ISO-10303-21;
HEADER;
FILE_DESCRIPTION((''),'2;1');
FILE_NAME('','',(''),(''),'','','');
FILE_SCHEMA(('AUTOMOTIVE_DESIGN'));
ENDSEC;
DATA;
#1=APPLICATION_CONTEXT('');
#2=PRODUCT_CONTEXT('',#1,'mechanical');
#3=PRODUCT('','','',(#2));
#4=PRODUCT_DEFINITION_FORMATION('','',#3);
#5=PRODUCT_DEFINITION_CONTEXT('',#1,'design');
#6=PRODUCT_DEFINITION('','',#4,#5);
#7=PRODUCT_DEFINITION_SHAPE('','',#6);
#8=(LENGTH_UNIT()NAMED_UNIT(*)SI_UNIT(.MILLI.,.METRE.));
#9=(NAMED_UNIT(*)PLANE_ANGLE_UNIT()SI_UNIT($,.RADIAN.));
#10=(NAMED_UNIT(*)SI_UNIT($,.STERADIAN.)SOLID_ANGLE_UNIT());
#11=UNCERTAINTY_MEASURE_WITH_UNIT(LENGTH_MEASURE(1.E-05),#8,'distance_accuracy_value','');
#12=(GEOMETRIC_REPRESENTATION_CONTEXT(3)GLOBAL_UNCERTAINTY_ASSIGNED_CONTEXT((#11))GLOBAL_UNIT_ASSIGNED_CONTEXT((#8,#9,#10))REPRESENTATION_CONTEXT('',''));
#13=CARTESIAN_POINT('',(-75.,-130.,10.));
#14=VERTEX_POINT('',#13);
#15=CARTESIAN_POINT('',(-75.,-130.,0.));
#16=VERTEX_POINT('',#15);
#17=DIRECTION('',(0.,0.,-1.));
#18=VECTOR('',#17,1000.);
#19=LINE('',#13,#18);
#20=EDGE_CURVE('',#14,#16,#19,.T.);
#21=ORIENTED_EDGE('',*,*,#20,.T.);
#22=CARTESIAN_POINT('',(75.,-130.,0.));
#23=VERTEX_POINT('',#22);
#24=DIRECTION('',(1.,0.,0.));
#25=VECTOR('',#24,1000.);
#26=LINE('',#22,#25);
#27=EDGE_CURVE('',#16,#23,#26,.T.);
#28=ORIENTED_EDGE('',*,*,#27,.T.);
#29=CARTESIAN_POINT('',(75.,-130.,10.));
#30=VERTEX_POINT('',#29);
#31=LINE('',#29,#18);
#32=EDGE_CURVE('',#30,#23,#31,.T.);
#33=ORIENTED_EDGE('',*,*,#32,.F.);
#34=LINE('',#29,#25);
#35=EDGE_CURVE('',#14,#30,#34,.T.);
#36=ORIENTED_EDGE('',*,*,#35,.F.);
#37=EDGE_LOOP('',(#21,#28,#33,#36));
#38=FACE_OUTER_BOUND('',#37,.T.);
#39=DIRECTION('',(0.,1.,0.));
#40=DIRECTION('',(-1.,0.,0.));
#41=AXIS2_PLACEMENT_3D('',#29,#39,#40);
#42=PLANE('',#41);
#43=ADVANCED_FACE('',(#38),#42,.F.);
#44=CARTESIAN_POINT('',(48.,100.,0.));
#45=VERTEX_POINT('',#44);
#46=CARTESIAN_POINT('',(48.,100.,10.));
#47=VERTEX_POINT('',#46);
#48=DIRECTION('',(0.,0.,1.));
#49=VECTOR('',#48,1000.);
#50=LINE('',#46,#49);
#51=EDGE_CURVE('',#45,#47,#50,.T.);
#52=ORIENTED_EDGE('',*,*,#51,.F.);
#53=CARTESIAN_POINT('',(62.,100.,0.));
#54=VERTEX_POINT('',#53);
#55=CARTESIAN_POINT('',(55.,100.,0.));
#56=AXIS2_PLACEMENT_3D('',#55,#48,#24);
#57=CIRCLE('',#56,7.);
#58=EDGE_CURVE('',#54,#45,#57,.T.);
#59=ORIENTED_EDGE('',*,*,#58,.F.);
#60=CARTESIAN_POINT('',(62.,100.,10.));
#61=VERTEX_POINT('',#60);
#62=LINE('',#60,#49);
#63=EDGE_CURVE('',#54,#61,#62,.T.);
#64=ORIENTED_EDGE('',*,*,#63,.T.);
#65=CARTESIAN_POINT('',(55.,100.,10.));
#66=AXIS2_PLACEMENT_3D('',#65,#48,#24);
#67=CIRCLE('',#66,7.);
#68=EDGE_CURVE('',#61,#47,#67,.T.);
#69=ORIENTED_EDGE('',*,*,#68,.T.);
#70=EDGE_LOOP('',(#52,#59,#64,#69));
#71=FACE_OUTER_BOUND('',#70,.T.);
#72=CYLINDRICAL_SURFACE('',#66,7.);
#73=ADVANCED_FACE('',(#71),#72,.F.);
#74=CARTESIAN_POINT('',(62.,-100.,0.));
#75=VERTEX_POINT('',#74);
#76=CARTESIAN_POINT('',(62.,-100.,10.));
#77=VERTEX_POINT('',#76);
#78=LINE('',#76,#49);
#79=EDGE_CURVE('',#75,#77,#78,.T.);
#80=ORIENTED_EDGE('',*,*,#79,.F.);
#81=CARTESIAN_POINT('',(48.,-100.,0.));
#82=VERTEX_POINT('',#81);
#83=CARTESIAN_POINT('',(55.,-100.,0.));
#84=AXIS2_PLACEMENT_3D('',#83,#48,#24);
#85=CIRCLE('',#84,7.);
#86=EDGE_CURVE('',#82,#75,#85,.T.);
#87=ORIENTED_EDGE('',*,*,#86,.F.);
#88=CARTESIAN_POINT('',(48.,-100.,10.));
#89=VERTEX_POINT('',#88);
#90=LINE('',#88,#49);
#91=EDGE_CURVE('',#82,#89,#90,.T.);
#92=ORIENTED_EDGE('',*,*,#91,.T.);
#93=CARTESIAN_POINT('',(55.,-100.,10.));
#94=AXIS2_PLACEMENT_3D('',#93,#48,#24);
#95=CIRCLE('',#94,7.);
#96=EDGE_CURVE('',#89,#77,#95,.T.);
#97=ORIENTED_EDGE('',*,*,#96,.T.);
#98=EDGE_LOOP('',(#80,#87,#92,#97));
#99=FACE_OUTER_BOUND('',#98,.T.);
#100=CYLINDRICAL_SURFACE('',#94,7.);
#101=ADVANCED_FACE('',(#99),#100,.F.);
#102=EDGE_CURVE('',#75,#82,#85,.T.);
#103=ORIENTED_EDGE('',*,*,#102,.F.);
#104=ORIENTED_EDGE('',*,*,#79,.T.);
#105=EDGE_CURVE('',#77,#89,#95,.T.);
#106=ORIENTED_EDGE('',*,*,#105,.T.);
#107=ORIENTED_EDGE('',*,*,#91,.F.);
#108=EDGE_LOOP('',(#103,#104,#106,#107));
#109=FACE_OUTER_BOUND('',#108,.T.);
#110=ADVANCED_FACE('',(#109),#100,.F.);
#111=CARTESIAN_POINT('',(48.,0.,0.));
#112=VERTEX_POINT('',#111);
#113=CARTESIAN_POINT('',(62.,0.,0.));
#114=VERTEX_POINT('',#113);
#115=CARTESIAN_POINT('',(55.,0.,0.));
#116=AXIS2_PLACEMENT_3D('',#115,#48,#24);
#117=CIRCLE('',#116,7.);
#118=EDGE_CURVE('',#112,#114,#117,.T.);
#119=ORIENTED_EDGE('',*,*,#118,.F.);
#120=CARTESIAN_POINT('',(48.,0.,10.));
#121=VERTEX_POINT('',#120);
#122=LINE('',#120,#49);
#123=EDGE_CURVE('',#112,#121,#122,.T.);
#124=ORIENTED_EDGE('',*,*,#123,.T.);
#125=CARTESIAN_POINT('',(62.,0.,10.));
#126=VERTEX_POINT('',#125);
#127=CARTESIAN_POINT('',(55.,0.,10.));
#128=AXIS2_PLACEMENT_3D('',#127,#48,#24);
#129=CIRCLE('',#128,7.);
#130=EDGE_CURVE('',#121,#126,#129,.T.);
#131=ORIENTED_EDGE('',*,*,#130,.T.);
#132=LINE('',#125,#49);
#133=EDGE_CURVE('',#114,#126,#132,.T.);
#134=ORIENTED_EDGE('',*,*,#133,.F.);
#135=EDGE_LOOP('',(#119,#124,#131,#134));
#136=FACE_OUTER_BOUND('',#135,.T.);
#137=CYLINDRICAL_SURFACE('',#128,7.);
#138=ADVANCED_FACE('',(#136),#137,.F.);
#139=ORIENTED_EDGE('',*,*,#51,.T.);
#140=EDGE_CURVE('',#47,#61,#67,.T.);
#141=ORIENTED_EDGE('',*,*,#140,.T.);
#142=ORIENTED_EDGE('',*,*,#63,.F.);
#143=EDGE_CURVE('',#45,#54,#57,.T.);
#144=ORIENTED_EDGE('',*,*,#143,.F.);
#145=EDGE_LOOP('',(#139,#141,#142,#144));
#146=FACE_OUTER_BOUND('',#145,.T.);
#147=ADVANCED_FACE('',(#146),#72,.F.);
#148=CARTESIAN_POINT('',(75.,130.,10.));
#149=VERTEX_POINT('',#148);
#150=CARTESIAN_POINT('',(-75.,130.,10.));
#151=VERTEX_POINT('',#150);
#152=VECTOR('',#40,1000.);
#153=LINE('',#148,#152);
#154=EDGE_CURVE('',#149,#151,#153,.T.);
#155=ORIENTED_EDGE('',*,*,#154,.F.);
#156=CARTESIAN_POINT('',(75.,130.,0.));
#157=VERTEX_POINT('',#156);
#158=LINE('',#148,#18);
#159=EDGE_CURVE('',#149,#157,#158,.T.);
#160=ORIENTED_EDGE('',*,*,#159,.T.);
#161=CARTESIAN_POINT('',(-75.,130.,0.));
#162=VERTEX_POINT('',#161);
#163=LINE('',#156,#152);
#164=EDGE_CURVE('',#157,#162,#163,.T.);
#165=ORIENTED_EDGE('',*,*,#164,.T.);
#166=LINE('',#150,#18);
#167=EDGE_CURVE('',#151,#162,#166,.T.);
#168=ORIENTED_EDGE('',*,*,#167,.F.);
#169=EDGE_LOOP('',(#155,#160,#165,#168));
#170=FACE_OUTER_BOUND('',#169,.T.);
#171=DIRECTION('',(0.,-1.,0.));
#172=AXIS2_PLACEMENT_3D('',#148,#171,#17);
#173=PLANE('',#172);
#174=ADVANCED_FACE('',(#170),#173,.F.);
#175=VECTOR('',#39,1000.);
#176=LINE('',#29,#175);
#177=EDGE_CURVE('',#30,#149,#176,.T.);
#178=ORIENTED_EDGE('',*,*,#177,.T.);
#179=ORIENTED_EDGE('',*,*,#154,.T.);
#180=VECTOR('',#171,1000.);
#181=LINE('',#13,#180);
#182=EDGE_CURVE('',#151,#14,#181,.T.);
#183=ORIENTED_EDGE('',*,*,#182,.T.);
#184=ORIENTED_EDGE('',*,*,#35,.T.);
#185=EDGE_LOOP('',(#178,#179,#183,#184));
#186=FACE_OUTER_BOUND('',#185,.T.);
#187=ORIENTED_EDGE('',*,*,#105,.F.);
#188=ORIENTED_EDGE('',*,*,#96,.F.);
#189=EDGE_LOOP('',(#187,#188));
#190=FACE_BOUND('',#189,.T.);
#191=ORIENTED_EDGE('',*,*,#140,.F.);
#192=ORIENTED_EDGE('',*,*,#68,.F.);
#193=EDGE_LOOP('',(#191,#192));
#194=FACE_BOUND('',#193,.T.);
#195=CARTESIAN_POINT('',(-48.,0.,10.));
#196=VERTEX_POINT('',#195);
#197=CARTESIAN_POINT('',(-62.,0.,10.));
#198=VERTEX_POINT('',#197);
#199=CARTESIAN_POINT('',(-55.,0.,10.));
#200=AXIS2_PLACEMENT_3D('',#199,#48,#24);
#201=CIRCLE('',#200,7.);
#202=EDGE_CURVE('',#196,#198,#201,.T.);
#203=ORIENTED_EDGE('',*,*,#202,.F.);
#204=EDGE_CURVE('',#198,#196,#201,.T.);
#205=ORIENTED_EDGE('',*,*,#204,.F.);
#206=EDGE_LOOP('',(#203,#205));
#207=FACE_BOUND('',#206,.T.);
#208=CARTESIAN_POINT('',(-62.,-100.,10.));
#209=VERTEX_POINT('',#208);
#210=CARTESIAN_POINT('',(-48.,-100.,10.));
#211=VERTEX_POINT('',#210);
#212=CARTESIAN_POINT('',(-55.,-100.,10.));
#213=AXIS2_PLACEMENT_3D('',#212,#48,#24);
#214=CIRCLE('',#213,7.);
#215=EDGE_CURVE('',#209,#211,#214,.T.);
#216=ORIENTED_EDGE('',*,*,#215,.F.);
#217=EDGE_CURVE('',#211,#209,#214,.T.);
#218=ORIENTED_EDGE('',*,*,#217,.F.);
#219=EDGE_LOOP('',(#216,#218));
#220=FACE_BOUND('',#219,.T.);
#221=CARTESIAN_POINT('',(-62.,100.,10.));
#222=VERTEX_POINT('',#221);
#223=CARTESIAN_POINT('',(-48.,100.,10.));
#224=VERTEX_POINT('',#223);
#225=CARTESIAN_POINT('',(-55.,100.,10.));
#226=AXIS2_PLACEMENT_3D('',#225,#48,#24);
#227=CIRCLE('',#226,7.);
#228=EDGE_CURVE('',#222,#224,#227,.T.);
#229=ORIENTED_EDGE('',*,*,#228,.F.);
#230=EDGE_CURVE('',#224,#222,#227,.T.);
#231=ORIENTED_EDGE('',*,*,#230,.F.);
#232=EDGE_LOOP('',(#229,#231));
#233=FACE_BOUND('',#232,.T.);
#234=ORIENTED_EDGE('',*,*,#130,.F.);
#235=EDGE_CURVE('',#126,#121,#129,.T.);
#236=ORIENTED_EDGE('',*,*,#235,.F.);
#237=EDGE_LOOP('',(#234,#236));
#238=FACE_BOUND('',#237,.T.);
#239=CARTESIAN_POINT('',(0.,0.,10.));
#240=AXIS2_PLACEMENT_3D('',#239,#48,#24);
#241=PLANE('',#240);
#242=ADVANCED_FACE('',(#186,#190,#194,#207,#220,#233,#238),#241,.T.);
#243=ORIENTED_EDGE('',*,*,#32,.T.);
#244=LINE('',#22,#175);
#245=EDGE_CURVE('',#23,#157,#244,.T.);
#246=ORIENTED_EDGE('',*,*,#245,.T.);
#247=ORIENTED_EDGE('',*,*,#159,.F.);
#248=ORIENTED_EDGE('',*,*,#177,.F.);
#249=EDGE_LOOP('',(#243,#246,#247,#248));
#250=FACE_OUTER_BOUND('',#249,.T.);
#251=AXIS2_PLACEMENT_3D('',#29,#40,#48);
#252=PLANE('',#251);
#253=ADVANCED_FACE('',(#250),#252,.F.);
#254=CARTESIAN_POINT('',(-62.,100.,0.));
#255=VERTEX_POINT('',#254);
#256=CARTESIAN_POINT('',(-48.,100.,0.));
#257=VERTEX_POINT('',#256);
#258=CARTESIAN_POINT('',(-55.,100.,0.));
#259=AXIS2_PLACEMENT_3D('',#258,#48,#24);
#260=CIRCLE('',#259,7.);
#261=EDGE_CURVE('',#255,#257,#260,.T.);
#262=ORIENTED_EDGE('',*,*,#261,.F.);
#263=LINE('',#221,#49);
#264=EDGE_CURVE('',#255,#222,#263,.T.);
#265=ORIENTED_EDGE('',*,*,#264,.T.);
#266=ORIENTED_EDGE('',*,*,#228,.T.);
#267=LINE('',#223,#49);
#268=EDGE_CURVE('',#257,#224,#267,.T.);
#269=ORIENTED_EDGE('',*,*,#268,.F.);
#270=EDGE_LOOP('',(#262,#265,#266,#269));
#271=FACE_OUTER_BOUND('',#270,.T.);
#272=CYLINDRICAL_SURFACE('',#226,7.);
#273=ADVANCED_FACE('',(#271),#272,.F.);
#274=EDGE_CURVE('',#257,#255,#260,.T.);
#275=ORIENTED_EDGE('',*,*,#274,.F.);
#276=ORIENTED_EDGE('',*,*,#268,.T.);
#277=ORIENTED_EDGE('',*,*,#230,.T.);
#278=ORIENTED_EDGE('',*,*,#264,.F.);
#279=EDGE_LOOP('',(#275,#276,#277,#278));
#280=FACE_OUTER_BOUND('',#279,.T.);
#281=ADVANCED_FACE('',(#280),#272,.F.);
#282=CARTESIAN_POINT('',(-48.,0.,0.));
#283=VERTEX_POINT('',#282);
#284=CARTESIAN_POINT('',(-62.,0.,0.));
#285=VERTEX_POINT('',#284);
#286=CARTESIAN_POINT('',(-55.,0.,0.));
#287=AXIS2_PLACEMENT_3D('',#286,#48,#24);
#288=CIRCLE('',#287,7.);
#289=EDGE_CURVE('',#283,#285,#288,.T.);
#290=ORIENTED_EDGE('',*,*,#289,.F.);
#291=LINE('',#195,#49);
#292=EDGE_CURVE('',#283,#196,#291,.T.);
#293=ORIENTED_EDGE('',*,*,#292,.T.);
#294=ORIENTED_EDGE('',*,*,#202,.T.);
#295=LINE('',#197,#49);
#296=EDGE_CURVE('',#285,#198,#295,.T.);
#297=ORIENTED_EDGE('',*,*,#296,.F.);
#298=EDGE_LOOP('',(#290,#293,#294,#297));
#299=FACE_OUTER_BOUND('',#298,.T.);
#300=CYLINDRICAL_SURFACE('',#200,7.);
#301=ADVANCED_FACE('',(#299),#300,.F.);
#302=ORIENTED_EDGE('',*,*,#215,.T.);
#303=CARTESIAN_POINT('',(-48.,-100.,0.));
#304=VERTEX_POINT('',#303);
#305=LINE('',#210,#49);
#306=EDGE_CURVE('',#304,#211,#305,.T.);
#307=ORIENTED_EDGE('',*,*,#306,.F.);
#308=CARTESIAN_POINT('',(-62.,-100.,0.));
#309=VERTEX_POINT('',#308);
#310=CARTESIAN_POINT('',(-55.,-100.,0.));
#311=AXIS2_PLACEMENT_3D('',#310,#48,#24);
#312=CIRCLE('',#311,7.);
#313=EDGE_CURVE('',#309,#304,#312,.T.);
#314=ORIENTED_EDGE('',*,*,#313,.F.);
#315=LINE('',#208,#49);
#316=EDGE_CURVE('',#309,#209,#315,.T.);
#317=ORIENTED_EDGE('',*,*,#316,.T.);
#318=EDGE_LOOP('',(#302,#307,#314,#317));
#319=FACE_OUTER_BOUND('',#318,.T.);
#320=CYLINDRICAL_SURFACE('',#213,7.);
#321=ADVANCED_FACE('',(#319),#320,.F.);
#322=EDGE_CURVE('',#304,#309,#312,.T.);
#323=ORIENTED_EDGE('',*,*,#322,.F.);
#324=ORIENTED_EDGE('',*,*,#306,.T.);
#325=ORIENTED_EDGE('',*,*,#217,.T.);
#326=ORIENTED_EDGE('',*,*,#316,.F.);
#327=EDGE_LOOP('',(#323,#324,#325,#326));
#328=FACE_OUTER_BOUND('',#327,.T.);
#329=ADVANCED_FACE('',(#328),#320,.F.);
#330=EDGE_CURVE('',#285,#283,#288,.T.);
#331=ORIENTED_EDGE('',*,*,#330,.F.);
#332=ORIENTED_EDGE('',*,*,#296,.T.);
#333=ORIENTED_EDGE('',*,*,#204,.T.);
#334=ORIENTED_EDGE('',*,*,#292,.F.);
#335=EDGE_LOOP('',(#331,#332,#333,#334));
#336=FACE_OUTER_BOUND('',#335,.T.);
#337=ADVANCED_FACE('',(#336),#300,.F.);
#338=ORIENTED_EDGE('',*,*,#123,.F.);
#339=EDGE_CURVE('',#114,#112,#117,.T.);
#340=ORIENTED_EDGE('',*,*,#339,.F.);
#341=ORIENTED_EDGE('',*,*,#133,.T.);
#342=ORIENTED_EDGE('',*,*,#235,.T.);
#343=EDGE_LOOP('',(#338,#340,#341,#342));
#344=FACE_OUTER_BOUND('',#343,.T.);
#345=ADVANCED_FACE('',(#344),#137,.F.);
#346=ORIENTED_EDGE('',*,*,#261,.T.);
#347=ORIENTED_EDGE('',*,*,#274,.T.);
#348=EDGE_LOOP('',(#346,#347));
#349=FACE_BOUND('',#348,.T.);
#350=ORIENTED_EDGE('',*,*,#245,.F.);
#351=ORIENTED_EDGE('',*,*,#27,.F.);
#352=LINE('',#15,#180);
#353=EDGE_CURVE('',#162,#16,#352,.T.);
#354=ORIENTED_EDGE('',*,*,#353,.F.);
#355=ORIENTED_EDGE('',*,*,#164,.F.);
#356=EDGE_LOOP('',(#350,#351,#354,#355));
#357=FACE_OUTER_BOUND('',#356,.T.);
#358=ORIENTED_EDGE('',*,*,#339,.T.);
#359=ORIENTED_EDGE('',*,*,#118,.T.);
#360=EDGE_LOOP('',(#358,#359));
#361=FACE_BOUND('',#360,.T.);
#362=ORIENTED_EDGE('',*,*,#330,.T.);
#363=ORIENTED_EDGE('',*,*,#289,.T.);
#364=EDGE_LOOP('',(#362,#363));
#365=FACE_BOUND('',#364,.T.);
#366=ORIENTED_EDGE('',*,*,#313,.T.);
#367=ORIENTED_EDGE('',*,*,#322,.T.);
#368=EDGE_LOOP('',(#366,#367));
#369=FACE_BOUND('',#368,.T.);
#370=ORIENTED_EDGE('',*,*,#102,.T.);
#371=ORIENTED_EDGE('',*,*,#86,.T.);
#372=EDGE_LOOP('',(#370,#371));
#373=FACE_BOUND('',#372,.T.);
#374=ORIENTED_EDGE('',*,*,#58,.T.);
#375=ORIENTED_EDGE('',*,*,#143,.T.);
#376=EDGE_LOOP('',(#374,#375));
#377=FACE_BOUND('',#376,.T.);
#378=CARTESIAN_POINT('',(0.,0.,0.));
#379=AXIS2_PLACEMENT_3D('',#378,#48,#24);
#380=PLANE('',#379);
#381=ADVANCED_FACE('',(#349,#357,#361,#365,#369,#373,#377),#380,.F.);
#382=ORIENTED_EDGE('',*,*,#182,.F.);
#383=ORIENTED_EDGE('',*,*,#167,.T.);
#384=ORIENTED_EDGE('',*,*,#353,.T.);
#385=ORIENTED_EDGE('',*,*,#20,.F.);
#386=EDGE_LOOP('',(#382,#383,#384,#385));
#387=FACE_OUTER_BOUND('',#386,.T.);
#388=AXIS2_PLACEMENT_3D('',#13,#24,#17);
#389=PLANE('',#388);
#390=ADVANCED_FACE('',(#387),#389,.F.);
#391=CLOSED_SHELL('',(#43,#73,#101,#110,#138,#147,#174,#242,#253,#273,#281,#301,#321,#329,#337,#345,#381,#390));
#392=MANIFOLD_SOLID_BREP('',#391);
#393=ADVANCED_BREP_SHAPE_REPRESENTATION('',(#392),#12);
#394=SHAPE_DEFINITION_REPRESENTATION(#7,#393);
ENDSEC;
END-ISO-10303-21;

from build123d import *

# Parameters (mm, degrees)
SKETCH1_W                  = 150
SKETCH1_H                  = 260
BOSS_EXTRUDE1_DEPTH        = 10
F_14_0_14_DIAMETER_HOLE1_D = 14


with BuildPart() as part:
    # Sketch1 → Boss-Extrude1 (new body)
    with BuildSketch(Plane.XY):
        Rectangle(SKETCH1_W, SKETCH1_H)
    extrude(amount=BOSS_EXTRUDE1_DEPTH)

    # Ø14.0 (14) Diameter Hole1 (through all)
    with Locations(Plane.XY.offset(10)):
        with Locations((-55, 100), (-55, 0), (-55, -100), (55, -100), (55, 0), (55, 100)):
            Hole(F_14_0_14_DIAMETER_HOLE1_D / 2)


solid = part.part
